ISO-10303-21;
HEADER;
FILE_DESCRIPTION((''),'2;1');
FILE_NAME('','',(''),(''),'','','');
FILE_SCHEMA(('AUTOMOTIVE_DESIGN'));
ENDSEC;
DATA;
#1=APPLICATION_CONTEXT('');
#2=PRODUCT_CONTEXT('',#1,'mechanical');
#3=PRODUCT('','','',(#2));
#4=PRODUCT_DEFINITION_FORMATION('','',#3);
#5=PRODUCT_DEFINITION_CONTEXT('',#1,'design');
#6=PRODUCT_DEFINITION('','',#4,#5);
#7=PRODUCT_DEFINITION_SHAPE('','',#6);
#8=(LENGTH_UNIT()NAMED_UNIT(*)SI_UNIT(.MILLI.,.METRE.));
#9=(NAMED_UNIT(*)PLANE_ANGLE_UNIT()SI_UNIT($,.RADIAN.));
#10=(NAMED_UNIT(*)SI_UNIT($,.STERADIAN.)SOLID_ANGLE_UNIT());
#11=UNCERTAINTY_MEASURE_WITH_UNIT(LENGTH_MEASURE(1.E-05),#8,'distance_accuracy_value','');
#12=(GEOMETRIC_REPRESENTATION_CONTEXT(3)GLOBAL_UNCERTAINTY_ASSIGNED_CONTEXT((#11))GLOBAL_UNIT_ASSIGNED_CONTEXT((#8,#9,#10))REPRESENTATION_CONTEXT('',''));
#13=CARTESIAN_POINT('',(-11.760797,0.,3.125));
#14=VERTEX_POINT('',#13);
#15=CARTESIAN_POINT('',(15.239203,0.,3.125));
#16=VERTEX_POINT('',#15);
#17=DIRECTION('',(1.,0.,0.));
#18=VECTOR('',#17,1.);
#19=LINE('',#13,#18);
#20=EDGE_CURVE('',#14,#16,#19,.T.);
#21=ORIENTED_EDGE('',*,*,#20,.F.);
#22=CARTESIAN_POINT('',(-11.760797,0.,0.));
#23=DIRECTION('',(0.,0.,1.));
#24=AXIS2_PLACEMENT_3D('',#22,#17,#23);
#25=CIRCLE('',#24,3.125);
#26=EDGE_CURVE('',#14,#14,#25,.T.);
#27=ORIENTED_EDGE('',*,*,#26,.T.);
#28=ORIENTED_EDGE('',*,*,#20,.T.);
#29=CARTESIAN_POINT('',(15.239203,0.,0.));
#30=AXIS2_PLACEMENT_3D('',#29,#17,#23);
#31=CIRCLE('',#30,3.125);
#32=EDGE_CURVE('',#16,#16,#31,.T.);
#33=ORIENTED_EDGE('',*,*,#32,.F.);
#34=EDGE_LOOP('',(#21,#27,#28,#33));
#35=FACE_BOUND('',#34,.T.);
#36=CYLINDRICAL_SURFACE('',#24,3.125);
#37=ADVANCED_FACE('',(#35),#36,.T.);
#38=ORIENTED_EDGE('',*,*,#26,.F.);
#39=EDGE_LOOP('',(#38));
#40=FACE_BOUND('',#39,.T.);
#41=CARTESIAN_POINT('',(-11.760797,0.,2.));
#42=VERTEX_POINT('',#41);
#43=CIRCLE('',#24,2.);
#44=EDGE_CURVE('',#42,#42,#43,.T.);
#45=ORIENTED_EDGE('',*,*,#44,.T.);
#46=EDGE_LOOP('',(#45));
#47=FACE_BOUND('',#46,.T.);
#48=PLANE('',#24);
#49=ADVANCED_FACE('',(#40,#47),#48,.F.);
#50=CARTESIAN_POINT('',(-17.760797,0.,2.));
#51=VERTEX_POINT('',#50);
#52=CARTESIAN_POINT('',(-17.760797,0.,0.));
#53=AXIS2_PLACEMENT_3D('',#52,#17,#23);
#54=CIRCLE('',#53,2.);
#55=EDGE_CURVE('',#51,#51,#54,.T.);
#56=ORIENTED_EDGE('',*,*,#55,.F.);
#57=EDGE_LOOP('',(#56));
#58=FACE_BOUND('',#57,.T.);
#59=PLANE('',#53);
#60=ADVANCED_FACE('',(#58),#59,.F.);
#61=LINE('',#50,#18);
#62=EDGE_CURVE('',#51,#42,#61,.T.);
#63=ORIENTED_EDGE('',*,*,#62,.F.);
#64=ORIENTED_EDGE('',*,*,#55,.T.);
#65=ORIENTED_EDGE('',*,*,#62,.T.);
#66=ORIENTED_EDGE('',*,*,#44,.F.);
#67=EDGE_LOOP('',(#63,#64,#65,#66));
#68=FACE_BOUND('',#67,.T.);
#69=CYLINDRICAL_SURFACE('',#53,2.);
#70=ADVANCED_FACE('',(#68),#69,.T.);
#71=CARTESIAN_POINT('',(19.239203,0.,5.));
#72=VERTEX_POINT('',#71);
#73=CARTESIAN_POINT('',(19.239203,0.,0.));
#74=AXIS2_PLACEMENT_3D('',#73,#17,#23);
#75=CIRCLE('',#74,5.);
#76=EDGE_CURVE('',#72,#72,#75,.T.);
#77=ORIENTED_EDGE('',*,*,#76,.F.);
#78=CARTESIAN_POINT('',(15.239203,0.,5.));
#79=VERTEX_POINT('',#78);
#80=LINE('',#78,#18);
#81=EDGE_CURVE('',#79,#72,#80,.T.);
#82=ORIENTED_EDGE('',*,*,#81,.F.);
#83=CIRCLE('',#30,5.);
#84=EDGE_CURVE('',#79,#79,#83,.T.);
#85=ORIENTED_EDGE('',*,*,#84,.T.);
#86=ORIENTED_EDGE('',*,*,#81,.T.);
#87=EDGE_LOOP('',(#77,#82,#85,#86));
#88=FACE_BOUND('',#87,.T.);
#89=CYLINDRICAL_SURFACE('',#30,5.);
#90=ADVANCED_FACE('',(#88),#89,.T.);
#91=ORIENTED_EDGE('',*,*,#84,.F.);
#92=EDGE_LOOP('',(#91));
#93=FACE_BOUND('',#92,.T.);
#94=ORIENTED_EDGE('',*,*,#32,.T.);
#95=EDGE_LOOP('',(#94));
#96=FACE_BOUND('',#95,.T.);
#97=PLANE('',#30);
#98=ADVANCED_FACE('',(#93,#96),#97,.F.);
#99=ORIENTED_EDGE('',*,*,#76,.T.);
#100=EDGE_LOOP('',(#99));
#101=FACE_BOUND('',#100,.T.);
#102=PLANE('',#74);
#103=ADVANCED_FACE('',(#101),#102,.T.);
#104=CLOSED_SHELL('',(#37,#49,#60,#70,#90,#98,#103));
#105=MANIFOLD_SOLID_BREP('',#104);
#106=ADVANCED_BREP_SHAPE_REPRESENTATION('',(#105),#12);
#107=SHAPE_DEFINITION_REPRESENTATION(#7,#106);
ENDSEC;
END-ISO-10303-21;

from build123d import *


with BuildPart() as part:
    # Sketch1 → Revolve1 (revolve)
    with BuildSketch(Plane.XY, mode=Mode.PRIVATE) as revolve1_sk:
        Polygon((-17.760797342, 0), (-17.760797342, -2), (-11.760797342, -2), (-11.760797342, -3.125), (15.239202658, -3.125), (15.239202658, -5), (19.239202658, -5), (19.239202658, 0), align=None)
    revolve(revolve1_sk.sketch.rotate(Axis((-26.641196013, 0, 0), (1, 0, 0)), 270), axis=Axis((-26.641196013, 0, 0), (1, 0, 0)))


solid = part.part
